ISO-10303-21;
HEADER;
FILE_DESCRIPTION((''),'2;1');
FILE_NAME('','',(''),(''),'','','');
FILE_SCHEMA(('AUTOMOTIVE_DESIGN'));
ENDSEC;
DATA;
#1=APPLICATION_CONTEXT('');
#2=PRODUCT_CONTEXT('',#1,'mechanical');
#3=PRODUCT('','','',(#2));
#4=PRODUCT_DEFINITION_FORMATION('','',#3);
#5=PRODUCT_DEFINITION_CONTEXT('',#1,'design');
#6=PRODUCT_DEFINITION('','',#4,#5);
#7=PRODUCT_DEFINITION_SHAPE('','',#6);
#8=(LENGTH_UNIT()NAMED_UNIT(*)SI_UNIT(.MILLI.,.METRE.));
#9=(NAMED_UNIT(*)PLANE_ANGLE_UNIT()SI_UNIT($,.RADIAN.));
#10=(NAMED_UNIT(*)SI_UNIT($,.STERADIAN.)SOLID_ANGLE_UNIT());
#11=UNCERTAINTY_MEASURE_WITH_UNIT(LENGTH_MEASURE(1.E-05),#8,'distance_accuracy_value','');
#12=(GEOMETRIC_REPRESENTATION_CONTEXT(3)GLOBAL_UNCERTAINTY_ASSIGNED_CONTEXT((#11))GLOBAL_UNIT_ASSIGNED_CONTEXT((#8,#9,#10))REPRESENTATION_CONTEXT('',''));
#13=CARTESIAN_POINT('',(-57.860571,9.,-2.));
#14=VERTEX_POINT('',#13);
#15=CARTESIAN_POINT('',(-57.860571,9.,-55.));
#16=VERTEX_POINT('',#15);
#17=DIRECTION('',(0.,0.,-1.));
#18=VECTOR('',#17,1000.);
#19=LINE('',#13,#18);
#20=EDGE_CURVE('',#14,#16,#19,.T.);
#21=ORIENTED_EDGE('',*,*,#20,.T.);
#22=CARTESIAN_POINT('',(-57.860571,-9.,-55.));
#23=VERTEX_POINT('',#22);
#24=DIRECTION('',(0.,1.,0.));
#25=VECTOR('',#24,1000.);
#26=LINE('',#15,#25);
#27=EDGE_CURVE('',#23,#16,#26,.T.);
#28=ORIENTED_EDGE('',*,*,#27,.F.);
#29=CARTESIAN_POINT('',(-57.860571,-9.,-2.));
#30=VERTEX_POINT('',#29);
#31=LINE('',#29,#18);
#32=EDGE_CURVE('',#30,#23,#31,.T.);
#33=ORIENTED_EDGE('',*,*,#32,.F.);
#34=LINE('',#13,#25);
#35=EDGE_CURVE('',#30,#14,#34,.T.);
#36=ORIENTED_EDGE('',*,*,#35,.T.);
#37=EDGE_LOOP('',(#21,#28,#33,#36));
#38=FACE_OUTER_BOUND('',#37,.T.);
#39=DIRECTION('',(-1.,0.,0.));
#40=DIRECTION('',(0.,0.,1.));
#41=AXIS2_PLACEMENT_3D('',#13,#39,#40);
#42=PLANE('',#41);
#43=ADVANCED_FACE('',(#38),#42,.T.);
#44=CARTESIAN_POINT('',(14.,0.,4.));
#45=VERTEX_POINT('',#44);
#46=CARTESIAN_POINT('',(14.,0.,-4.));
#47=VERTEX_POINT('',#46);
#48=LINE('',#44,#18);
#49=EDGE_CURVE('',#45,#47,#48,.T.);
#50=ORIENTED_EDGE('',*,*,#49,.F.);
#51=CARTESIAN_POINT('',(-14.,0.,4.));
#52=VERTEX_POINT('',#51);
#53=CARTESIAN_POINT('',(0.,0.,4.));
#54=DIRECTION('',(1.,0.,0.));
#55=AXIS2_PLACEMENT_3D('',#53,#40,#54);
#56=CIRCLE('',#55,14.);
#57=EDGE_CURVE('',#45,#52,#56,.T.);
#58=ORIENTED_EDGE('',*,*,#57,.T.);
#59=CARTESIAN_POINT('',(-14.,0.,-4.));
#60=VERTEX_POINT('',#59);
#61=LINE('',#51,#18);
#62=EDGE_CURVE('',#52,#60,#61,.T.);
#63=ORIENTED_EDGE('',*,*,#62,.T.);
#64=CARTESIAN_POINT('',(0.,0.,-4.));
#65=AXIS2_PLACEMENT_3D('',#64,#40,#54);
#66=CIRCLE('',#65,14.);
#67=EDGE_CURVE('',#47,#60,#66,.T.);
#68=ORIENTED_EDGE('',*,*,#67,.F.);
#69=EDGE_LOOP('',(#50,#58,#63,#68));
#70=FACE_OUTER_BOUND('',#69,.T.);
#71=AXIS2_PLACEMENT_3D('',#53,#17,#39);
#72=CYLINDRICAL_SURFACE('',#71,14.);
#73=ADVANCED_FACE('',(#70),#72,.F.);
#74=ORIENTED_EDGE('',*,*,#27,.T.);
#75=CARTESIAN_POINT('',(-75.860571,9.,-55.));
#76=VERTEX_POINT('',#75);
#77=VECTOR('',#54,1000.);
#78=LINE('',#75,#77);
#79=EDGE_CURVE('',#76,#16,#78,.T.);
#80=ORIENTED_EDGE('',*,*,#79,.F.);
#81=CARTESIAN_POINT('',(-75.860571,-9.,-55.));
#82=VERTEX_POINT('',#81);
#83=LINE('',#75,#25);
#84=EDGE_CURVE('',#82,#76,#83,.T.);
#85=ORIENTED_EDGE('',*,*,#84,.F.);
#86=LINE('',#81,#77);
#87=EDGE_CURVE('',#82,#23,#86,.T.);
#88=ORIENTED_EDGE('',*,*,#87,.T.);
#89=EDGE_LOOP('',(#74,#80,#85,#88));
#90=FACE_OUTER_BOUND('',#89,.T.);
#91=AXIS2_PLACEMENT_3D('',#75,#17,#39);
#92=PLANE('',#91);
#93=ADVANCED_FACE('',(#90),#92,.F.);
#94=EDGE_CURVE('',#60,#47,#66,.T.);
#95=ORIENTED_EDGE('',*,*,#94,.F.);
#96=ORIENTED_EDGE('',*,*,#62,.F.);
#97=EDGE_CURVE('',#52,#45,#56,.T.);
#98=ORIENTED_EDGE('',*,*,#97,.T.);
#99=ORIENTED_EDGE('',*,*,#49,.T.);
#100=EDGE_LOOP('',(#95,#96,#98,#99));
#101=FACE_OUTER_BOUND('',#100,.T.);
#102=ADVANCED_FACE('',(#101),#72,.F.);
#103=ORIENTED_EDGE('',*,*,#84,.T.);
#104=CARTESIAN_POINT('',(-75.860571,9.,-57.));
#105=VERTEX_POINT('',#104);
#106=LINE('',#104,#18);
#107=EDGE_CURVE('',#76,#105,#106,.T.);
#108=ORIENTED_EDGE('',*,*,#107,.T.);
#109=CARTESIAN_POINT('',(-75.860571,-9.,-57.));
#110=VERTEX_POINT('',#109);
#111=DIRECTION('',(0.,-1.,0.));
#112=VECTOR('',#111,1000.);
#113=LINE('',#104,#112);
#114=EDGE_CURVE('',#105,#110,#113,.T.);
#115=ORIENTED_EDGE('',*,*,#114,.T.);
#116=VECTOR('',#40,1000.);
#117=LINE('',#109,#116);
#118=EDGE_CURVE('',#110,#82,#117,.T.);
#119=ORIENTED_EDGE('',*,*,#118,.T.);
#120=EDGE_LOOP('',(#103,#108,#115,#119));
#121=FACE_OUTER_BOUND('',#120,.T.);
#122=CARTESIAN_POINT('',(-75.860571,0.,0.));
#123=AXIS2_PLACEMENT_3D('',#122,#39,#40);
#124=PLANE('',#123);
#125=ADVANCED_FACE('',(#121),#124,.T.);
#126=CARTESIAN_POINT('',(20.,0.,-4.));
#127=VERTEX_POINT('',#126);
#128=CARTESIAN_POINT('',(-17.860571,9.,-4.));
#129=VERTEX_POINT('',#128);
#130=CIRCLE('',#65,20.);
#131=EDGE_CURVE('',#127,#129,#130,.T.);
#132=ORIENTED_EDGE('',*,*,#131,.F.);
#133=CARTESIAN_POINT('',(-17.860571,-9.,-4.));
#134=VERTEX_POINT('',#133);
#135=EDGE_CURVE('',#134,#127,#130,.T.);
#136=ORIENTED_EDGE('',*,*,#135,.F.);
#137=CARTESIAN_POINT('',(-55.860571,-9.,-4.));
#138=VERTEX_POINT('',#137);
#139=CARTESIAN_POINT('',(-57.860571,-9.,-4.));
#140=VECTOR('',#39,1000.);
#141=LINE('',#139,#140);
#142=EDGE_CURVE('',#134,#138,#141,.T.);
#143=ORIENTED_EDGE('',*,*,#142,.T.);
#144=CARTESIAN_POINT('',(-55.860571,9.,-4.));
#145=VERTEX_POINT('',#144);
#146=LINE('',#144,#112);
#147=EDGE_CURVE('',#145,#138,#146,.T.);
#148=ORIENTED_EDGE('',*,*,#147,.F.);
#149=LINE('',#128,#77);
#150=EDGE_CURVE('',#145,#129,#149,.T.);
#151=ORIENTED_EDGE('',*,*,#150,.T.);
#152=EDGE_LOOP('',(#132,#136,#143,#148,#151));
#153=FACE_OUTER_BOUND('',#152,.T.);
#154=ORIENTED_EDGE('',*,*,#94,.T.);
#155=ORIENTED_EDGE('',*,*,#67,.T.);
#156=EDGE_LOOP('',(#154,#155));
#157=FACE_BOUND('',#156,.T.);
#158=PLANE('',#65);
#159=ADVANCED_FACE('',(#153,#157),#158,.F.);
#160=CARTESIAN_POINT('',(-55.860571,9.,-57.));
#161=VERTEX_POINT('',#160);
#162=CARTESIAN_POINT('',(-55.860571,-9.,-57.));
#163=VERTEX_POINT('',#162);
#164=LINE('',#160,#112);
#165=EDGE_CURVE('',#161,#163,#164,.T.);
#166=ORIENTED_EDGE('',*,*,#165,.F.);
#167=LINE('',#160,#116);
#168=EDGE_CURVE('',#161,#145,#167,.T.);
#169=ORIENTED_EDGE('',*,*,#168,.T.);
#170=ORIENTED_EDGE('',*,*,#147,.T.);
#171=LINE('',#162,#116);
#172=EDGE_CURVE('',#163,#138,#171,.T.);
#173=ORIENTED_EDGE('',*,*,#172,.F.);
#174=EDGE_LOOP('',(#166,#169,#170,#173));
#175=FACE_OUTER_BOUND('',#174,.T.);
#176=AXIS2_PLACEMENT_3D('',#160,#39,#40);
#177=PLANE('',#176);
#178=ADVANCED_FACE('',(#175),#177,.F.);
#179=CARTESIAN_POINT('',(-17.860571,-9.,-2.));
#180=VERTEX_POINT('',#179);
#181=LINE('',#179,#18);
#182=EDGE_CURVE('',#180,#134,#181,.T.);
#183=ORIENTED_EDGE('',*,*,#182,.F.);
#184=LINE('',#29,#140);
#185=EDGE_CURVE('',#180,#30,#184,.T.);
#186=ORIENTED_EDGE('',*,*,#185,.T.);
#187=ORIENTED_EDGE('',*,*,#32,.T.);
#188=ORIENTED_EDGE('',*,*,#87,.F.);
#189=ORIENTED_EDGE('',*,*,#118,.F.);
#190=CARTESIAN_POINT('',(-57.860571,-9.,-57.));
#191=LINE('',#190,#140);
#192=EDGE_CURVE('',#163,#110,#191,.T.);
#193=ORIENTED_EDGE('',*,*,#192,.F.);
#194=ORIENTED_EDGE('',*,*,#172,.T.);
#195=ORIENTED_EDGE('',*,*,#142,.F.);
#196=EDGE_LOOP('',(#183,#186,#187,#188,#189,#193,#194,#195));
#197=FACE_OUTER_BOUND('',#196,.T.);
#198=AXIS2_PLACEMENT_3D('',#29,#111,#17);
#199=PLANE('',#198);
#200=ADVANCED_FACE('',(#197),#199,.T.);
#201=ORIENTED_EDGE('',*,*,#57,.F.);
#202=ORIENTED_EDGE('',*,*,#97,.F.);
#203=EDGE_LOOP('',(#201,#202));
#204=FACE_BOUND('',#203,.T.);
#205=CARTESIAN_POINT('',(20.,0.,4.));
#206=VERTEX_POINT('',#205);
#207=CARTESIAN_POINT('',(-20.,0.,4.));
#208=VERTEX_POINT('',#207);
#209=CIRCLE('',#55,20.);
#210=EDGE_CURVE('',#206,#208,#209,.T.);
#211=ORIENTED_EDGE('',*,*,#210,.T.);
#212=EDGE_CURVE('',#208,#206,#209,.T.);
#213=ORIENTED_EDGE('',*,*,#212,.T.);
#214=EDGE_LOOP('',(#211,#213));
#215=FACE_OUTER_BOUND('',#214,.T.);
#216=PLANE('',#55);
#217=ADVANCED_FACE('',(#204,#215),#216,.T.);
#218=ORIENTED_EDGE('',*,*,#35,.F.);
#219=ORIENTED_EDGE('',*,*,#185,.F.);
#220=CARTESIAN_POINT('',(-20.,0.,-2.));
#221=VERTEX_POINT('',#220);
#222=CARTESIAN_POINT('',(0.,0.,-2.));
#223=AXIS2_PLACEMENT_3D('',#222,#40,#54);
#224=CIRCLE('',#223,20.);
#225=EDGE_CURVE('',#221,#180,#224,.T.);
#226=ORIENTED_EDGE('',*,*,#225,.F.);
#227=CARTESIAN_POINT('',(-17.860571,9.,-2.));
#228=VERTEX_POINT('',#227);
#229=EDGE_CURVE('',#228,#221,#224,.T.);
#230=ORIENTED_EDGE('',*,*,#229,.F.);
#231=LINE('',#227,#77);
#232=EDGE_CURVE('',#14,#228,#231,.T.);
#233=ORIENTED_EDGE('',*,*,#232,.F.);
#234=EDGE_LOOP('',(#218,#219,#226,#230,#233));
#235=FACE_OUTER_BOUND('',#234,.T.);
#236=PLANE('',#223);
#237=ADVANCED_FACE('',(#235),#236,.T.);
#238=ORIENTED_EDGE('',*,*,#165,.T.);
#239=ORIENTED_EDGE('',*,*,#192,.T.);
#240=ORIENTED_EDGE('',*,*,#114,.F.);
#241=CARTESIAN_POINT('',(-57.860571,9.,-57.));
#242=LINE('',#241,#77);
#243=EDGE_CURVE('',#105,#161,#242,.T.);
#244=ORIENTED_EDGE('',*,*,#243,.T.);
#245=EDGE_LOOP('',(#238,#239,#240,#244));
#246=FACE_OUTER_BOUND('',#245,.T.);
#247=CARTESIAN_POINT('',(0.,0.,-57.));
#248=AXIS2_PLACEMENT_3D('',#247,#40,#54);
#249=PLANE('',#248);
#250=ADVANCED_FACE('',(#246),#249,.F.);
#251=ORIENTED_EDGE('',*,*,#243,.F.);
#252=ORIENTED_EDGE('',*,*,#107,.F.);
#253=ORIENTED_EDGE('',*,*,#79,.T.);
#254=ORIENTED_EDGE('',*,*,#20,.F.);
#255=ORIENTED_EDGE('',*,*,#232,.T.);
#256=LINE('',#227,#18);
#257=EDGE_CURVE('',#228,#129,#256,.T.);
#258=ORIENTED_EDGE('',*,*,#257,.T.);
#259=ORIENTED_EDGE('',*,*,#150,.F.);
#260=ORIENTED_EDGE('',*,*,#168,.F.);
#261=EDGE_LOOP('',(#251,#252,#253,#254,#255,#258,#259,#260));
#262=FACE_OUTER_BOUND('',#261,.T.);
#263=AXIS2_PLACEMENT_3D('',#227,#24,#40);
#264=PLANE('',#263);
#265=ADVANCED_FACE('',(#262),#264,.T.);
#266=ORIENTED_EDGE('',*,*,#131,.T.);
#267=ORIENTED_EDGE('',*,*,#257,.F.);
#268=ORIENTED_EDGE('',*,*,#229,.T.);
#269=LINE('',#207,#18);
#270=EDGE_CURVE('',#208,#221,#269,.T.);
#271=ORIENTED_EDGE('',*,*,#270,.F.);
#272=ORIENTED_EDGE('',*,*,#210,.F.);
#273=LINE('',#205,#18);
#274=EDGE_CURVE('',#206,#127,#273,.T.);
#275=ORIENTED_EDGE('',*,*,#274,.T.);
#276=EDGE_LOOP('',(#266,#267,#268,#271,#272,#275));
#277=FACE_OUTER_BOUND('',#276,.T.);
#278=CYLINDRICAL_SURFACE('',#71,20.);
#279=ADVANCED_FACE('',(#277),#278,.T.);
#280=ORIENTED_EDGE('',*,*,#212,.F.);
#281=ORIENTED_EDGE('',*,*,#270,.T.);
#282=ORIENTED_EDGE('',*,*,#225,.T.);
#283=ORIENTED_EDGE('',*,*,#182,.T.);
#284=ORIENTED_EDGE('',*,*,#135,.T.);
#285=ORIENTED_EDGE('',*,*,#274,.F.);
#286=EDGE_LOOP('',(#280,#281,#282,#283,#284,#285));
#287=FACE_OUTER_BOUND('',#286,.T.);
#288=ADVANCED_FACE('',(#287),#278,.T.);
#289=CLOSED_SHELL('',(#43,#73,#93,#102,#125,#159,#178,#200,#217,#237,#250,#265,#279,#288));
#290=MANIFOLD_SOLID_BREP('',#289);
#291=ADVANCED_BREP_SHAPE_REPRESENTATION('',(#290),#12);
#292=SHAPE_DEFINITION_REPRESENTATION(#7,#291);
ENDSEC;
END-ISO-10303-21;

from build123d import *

# Parameters (mm, degrees)
SKETCH_1_R      = 20
SKETCH_1_R_2    = 14
EXTRUDE_1_DEPTH = 4
SKETCH_2_W      = 40
SKETCH_2_H      = 18
EXTRUDE_2_DEPTH = 2
SKETCH_3_W      = 2
SKETCH_3_H      = 18
EXTRUDE_3_DEPTH = 53
SKETCH_4_W      = 2
SKETCH_4_H      = 18
EXTRUDE_4_DEPTH = 18


with BuildPart() as part:
    # 草图1 → 凸台-拉伸1 (new, symmetric)
    with BuildSketch(Plane.XY):
        Circle(SKETCH_1_R)
        Circle(SKETCH_1_R_2, mode=Mode.SUBTRACT)
    extrude(amount=EXTRUDE_1_DEPTH, both=True)

    # 草图2 → 凸台-拉伸2 (add)
    with BuildSketch(Plane(origin=(0, 0, -4), x_dir=(-1, 0, 0), z_dir=(0, 0, -1))):
        with Locations((37.860571099, 0)):
            Rectangle(SKETCH_2_W, SKETCH_2_H)
    extrude(amount=-EXTRUDE_2_DEPTH)

    # 草图3 → 凸台-拉伸3 (add)
    with BuildSketch(Plane(origin=(0, 0, -4), x_dir=(-1, 0, 0), z_dir=(0, 0, -1))):
        with Locations((56.860571099, 0)):
            Rectangle(SKETCH_3_W, SKETCH_3_H)
    extrude(amount=EXTRUDE_3_DEPTH)

    # 草图4 → 凸台-拉伸4 (add)
    with BuildSketch(Plane.ZY.offset(57.860571099)):
        with Locations((-56, 0)):
            Rectangle(SKETCH_4_W, SKETCH_4_H)
    extrude(amount=EXTRUDE_4_DEPTH)


solid = part.part
